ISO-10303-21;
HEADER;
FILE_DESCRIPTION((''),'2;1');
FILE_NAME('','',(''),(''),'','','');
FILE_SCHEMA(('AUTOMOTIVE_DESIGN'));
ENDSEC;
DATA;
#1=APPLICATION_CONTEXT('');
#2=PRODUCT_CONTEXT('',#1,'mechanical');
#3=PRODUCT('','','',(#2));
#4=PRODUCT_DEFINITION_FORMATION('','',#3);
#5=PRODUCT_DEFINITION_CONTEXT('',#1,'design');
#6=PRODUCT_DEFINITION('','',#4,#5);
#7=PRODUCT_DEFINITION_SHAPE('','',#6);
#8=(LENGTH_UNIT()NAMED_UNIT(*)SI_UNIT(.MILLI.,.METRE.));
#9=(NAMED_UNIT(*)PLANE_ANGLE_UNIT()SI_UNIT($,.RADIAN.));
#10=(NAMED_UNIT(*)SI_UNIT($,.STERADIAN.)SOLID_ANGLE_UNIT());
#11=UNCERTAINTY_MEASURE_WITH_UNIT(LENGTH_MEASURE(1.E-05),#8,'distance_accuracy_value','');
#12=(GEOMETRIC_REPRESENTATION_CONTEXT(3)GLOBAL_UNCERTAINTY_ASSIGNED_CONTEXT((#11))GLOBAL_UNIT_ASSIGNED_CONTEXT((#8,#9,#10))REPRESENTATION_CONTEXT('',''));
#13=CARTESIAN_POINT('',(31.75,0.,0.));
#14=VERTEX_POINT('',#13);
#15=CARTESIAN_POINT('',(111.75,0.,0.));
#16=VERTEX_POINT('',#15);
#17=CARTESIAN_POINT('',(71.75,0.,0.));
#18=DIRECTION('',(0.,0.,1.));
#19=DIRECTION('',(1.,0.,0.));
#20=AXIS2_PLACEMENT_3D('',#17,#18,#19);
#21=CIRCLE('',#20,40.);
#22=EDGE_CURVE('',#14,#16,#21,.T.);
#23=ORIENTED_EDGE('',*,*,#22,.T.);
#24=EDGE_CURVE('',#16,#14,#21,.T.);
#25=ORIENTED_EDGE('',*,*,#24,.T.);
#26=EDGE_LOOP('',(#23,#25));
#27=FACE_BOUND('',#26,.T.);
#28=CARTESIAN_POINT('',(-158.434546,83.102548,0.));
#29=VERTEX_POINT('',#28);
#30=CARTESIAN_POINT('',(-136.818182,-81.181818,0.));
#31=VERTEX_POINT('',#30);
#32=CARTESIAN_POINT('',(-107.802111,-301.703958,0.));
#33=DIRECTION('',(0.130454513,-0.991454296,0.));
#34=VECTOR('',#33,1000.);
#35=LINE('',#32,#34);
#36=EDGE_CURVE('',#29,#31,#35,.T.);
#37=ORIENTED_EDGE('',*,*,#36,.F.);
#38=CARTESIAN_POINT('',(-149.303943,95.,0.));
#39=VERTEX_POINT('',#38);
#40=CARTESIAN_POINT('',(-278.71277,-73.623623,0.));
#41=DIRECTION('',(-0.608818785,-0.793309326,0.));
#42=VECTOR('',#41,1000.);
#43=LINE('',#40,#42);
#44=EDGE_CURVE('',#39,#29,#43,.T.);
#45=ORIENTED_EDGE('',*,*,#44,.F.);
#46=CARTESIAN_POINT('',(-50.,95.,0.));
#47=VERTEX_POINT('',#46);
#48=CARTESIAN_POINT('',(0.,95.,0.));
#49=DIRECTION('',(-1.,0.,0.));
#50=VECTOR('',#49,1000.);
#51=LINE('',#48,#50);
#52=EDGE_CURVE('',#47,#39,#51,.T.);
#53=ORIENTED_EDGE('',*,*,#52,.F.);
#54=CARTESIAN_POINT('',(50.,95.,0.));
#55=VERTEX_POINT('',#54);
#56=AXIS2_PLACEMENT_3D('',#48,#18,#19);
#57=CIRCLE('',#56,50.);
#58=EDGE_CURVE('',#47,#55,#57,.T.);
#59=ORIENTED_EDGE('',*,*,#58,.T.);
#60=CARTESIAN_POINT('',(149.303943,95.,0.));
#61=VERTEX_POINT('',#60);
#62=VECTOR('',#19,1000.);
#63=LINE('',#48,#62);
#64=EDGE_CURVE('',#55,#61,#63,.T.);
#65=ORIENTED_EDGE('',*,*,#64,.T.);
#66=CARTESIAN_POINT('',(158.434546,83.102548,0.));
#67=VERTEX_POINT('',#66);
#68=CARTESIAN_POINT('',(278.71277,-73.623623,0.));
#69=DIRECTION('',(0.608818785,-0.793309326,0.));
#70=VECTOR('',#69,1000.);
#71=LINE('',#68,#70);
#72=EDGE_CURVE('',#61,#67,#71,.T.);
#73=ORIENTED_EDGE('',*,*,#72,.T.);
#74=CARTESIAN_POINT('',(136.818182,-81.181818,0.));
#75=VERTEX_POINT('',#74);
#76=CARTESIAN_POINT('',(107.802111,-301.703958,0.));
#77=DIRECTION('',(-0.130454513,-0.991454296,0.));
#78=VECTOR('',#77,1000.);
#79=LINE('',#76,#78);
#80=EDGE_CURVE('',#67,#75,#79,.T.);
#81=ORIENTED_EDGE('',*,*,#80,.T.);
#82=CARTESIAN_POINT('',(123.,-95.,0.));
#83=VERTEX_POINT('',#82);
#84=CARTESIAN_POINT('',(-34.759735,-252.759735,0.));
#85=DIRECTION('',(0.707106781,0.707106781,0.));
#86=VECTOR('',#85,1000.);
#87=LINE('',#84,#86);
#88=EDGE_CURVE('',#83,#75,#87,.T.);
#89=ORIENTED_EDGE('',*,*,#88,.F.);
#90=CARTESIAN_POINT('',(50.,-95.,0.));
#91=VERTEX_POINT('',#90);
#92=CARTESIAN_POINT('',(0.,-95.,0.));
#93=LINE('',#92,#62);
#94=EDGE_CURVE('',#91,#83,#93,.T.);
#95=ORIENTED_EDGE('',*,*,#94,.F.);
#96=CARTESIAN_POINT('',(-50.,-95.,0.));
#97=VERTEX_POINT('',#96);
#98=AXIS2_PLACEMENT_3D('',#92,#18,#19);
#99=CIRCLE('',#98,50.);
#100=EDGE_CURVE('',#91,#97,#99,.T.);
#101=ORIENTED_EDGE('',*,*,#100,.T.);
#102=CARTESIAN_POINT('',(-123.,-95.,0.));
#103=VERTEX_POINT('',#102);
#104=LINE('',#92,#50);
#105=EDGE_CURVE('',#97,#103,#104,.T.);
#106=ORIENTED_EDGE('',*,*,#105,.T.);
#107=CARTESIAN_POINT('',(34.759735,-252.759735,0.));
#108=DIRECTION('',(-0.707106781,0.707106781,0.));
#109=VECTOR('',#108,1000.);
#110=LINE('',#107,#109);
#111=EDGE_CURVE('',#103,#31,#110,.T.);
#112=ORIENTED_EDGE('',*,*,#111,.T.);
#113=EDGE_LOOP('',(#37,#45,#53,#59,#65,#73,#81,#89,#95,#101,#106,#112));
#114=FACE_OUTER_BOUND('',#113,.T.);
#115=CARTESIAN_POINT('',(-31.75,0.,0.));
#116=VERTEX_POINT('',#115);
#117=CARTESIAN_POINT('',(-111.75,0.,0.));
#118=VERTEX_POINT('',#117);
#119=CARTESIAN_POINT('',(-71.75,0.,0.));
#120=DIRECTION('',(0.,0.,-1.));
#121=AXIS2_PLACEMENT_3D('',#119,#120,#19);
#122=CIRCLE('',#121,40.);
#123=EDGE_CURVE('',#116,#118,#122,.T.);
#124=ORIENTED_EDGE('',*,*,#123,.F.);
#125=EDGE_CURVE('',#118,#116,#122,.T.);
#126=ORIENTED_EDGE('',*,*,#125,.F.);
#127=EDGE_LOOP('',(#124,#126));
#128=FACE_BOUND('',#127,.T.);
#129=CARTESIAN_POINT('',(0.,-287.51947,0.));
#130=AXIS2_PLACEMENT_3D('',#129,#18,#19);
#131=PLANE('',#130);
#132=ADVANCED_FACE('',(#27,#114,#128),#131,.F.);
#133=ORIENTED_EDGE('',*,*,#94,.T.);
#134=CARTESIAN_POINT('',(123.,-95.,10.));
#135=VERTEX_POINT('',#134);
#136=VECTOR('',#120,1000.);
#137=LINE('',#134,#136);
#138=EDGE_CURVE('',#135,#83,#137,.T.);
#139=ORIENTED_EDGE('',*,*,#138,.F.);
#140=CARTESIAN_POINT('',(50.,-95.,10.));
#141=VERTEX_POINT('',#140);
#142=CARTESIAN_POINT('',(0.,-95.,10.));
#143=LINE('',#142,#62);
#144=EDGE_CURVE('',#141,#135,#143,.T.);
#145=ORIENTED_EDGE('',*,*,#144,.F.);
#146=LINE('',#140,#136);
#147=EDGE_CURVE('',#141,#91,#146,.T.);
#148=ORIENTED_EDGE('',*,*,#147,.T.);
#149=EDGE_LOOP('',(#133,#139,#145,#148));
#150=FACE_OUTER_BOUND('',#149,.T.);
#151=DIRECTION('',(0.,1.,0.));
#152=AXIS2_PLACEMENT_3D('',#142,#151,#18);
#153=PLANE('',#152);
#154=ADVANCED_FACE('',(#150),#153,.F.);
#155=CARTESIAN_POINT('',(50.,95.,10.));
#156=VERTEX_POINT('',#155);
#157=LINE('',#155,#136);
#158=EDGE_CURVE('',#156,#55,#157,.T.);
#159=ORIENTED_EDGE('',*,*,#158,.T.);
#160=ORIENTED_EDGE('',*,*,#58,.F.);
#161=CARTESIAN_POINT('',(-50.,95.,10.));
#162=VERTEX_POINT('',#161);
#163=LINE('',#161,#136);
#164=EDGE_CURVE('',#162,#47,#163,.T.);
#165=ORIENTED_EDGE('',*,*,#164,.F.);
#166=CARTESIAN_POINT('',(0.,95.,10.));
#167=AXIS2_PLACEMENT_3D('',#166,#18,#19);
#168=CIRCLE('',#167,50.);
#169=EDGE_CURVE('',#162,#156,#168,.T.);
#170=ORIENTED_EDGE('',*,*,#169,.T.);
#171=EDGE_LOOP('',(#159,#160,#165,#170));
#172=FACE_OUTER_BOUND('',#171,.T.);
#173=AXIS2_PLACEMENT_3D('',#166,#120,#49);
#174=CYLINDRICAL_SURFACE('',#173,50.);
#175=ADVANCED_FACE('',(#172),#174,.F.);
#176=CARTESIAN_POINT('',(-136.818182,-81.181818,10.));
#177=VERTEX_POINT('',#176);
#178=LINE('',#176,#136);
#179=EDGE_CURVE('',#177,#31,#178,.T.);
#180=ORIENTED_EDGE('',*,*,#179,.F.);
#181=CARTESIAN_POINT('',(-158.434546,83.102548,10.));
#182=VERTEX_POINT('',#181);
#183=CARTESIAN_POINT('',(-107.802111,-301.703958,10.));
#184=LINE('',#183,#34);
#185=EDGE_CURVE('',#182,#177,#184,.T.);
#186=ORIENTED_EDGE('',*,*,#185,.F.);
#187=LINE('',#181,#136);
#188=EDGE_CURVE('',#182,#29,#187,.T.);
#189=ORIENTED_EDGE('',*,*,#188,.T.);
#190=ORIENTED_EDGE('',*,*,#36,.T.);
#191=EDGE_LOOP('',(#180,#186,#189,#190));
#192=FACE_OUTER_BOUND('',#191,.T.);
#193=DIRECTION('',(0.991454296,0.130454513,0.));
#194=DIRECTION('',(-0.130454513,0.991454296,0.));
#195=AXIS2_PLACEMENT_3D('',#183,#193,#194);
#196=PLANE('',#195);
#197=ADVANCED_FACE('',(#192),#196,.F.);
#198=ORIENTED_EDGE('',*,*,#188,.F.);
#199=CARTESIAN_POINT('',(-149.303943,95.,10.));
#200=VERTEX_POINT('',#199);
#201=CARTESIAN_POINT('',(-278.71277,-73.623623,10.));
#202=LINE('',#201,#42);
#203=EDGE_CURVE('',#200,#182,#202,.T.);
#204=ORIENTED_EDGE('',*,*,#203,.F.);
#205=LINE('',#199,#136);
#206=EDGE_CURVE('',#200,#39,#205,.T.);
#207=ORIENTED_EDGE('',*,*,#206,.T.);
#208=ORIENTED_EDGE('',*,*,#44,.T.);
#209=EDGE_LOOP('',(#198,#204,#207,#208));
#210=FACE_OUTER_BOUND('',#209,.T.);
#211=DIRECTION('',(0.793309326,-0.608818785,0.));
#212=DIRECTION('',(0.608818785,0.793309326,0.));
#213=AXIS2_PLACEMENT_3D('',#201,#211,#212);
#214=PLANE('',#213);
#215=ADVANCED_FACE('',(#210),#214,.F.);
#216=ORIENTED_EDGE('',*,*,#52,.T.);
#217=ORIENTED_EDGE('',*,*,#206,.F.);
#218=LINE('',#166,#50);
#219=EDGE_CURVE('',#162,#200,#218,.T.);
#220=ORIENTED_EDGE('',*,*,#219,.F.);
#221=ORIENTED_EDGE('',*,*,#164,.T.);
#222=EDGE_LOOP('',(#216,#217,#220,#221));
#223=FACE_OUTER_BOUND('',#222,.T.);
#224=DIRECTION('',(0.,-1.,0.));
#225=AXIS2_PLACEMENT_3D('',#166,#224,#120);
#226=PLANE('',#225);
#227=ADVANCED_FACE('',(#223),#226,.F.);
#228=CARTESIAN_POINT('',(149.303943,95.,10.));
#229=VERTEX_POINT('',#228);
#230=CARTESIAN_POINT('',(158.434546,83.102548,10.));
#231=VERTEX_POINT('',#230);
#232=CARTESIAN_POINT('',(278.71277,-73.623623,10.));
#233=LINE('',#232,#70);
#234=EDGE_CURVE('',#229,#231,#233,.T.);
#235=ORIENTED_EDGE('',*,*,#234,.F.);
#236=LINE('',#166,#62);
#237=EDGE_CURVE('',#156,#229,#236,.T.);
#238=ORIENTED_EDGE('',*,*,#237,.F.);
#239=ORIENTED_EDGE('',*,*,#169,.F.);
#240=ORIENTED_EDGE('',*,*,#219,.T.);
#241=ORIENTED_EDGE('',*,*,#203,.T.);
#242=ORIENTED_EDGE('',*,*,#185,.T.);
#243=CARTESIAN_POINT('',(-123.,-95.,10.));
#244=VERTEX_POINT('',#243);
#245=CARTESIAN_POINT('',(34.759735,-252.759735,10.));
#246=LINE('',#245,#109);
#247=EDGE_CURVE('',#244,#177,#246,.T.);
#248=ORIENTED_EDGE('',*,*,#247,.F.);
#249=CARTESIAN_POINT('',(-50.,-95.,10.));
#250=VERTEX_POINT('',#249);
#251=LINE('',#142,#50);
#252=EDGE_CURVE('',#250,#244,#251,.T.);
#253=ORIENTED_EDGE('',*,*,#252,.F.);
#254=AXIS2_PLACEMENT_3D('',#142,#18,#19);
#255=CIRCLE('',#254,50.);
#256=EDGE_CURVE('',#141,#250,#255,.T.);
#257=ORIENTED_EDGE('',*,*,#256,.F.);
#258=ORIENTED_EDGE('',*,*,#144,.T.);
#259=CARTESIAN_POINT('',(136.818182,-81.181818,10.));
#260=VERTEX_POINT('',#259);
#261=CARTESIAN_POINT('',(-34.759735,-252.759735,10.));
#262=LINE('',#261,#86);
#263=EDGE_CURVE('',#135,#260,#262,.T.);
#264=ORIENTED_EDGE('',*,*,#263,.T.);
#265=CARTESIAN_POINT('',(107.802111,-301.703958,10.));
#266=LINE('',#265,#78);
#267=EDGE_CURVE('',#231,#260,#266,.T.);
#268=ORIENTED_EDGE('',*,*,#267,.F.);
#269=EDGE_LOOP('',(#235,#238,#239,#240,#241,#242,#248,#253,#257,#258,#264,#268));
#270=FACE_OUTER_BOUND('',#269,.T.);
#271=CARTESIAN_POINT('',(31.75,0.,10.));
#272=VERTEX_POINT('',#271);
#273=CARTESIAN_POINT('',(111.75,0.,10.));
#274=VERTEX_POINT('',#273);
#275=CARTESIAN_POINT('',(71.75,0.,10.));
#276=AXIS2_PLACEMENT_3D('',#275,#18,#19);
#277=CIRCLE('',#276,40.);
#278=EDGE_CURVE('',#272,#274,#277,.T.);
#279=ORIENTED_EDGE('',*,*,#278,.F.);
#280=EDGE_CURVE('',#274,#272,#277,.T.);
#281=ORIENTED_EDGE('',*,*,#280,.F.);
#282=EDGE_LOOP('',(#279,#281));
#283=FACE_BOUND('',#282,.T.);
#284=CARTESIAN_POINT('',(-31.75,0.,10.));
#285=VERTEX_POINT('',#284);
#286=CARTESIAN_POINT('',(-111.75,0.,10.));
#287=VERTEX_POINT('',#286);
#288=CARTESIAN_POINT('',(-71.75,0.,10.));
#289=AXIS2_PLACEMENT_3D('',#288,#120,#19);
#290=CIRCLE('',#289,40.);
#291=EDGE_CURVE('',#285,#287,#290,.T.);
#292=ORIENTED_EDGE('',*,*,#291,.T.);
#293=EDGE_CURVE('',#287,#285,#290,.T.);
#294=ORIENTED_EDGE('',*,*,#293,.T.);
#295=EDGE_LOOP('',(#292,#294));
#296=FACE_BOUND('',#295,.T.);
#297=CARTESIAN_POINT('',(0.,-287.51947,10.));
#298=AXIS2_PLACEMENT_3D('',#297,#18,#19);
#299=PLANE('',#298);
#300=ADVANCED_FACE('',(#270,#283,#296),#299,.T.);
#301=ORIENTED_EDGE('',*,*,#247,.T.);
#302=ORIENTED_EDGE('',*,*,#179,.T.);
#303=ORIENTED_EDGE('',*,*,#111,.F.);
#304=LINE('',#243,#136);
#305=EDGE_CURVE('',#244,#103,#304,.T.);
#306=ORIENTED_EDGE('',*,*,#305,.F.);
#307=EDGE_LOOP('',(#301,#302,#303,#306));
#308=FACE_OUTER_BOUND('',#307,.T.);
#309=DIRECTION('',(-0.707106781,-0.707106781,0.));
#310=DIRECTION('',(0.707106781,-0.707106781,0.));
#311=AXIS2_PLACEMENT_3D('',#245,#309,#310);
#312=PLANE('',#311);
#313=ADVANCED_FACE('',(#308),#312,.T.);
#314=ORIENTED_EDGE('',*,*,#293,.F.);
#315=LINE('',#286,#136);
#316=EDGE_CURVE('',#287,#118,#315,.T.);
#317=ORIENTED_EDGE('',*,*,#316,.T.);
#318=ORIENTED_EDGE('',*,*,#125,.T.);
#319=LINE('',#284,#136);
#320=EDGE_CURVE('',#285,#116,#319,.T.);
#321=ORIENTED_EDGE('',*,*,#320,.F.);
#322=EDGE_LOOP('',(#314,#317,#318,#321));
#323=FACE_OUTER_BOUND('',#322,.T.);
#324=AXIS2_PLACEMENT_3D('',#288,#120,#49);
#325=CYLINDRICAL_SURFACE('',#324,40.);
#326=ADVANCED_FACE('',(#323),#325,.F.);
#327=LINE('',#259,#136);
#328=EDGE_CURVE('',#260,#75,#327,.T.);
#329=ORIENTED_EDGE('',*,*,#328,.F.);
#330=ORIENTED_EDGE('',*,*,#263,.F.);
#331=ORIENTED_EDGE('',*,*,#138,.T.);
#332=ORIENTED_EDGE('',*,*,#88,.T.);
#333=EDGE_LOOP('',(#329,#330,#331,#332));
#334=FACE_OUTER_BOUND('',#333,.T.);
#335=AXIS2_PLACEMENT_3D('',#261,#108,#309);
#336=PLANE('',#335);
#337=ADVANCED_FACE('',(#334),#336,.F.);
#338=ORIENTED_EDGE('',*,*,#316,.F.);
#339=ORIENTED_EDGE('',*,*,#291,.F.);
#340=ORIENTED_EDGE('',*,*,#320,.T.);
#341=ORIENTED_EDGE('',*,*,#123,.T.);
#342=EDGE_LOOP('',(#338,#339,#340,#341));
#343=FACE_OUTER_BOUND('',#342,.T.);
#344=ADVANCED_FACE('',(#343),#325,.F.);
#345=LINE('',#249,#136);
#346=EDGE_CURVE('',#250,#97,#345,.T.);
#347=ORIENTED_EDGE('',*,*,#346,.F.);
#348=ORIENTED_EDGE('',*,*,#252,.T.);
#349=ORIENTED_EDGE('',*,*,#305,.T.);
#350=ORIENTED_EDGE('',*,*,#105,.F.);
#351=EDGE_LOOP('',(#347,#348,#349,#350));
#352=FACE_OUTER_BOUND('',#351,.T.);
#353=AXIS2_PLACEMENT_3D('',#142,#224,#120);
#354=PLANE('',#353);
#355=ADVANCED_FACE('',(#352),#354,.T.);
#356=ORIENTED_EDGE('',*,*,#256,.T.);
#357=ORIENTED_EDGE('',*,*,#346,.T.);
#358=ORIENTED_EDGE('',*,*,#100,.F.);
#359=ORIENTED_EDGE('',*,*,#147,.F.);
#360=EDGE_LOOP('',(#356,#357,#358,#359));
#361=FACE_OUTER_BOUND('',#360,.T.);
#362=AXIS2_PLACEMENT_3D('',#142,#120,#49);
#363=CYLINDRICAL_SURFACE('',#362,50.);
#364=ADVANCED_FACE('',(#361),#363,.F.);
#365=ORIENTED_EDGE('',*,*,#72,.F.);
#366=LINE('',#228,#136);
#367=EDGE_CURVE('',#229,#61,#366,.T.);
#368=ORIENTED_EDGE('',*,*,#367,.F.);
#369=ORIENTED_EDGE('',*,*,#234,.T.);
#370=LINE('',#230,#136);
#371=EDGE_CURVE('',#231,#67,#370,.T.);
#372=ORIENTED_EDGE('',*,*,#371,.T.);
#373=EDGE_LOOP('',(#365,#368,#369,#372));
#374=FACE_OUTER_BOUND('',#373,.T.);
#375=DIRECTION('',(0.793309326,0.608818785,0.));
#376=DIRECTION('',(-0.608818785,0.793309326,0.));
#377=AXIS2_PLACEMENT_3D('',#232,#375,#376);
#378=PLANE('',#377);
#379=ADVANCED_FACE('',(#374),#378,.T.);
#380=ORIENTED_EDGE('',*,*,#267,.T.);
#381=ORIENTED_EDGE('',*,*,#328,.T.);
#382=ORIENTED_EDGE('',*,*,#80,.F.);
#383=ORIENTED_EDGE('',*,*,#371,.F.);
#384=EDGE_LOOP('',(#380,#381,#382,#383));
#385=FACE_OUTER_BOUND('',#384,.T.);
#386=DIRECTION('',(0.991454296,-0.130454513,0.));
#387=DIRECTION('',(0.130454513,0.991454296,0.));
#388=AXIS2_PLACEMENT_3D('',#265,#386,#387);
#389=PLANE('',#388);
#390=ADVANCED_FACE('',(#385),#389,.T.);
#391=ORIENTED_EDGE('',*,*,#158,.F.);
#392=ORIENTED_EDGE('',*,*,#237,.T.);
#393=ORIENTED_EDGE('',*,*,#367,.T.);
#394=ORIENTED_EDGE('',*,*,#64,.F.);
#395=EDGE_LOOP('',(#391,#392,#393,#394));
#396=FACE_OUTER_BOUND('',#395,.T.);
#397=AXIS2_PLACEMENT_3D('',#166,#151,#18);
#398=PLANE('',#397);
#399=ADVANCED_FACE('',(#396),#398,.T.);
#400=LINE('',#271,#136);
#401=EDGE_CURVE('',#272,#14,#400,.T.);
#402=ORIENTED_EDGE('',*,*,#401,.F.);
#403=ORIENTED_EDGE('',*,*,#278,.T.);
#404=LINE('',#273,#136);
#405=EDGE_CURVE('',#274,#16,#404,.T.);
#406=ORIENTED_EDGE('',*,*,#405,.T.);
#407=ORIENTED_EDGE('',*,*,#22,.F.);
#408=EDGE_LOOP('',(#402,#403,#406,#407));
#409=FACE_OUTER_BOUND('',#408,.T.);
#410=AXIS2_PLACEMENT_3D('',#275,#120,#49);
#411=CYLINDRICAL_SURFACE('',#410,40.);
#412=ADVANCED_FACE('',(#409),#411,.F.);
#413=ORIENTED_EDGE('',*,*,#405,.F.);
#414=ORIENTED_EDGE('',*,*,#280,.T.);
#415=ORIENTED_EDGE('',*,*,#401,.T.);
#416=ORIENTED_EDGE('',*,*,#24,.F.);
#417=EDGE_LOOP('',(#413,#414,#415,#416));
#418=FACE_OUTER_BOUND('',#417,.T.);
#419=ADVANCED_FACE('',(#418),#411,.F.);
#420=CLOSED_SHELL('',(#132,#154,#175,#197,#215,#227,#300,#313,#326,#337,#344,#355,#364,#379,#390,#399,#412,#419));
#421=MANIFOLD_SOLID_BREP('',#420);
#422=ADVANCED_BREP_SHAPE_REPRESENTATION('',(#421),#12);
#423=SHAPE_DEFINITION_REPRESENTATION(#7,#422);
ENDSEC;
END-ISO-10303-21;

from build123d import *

# Parameters (mm, degrees)
SKETCH1_R           = 40
BOSS_EXTRUDE1_DEPTH = 10


with BuildPart() as part:
    # Sketch1 → Boss-Extrude1 (new body)
    with BuildSketch(Plane.XY):
        with BuildLine():
            Line((149.303943499, 95), (50, 95))
            ThreePointArc((50, 95), (0, 45), (-50, 95))
            Line((-50, 95), (-149.303943499, 95))
            Line((-149.303943499, 95), (-158.434545849, 83.102548453))
            Line((-158.434545849, 83.102548453), (-136.818181818, -81.181818182))
            Line((-136.818181818, -81.181818182), (-123, -95))
            Line((-123, -95), (-50.051564514, -95))
            Line((-50.051564514, -95), (-50, -95))
            ThreePointArc((-50, -95), (0, -45), (50, -95))
            Line((50, -95), (123, -95))
            Line((123, -95), (136.818181818, -81.181818182))
            Line((136.818181818, -81.181818182), (158.434545849, 83.102548453))
            Line((158.434545849, 83.102548453), (149.303943499, 95))
        make_face()
        with Locations((-71.75, 0)):
            Circle(SKETCH1_R, mode=Mode.SUBTRACT)
        with Locations((71.75, 0)):
            Circle(SKETCH1_R, mode=Mode.SUBTRACT)
    extrude(amount=BOSS_EXTRUDE1_DEPTH)


solid = part.part
